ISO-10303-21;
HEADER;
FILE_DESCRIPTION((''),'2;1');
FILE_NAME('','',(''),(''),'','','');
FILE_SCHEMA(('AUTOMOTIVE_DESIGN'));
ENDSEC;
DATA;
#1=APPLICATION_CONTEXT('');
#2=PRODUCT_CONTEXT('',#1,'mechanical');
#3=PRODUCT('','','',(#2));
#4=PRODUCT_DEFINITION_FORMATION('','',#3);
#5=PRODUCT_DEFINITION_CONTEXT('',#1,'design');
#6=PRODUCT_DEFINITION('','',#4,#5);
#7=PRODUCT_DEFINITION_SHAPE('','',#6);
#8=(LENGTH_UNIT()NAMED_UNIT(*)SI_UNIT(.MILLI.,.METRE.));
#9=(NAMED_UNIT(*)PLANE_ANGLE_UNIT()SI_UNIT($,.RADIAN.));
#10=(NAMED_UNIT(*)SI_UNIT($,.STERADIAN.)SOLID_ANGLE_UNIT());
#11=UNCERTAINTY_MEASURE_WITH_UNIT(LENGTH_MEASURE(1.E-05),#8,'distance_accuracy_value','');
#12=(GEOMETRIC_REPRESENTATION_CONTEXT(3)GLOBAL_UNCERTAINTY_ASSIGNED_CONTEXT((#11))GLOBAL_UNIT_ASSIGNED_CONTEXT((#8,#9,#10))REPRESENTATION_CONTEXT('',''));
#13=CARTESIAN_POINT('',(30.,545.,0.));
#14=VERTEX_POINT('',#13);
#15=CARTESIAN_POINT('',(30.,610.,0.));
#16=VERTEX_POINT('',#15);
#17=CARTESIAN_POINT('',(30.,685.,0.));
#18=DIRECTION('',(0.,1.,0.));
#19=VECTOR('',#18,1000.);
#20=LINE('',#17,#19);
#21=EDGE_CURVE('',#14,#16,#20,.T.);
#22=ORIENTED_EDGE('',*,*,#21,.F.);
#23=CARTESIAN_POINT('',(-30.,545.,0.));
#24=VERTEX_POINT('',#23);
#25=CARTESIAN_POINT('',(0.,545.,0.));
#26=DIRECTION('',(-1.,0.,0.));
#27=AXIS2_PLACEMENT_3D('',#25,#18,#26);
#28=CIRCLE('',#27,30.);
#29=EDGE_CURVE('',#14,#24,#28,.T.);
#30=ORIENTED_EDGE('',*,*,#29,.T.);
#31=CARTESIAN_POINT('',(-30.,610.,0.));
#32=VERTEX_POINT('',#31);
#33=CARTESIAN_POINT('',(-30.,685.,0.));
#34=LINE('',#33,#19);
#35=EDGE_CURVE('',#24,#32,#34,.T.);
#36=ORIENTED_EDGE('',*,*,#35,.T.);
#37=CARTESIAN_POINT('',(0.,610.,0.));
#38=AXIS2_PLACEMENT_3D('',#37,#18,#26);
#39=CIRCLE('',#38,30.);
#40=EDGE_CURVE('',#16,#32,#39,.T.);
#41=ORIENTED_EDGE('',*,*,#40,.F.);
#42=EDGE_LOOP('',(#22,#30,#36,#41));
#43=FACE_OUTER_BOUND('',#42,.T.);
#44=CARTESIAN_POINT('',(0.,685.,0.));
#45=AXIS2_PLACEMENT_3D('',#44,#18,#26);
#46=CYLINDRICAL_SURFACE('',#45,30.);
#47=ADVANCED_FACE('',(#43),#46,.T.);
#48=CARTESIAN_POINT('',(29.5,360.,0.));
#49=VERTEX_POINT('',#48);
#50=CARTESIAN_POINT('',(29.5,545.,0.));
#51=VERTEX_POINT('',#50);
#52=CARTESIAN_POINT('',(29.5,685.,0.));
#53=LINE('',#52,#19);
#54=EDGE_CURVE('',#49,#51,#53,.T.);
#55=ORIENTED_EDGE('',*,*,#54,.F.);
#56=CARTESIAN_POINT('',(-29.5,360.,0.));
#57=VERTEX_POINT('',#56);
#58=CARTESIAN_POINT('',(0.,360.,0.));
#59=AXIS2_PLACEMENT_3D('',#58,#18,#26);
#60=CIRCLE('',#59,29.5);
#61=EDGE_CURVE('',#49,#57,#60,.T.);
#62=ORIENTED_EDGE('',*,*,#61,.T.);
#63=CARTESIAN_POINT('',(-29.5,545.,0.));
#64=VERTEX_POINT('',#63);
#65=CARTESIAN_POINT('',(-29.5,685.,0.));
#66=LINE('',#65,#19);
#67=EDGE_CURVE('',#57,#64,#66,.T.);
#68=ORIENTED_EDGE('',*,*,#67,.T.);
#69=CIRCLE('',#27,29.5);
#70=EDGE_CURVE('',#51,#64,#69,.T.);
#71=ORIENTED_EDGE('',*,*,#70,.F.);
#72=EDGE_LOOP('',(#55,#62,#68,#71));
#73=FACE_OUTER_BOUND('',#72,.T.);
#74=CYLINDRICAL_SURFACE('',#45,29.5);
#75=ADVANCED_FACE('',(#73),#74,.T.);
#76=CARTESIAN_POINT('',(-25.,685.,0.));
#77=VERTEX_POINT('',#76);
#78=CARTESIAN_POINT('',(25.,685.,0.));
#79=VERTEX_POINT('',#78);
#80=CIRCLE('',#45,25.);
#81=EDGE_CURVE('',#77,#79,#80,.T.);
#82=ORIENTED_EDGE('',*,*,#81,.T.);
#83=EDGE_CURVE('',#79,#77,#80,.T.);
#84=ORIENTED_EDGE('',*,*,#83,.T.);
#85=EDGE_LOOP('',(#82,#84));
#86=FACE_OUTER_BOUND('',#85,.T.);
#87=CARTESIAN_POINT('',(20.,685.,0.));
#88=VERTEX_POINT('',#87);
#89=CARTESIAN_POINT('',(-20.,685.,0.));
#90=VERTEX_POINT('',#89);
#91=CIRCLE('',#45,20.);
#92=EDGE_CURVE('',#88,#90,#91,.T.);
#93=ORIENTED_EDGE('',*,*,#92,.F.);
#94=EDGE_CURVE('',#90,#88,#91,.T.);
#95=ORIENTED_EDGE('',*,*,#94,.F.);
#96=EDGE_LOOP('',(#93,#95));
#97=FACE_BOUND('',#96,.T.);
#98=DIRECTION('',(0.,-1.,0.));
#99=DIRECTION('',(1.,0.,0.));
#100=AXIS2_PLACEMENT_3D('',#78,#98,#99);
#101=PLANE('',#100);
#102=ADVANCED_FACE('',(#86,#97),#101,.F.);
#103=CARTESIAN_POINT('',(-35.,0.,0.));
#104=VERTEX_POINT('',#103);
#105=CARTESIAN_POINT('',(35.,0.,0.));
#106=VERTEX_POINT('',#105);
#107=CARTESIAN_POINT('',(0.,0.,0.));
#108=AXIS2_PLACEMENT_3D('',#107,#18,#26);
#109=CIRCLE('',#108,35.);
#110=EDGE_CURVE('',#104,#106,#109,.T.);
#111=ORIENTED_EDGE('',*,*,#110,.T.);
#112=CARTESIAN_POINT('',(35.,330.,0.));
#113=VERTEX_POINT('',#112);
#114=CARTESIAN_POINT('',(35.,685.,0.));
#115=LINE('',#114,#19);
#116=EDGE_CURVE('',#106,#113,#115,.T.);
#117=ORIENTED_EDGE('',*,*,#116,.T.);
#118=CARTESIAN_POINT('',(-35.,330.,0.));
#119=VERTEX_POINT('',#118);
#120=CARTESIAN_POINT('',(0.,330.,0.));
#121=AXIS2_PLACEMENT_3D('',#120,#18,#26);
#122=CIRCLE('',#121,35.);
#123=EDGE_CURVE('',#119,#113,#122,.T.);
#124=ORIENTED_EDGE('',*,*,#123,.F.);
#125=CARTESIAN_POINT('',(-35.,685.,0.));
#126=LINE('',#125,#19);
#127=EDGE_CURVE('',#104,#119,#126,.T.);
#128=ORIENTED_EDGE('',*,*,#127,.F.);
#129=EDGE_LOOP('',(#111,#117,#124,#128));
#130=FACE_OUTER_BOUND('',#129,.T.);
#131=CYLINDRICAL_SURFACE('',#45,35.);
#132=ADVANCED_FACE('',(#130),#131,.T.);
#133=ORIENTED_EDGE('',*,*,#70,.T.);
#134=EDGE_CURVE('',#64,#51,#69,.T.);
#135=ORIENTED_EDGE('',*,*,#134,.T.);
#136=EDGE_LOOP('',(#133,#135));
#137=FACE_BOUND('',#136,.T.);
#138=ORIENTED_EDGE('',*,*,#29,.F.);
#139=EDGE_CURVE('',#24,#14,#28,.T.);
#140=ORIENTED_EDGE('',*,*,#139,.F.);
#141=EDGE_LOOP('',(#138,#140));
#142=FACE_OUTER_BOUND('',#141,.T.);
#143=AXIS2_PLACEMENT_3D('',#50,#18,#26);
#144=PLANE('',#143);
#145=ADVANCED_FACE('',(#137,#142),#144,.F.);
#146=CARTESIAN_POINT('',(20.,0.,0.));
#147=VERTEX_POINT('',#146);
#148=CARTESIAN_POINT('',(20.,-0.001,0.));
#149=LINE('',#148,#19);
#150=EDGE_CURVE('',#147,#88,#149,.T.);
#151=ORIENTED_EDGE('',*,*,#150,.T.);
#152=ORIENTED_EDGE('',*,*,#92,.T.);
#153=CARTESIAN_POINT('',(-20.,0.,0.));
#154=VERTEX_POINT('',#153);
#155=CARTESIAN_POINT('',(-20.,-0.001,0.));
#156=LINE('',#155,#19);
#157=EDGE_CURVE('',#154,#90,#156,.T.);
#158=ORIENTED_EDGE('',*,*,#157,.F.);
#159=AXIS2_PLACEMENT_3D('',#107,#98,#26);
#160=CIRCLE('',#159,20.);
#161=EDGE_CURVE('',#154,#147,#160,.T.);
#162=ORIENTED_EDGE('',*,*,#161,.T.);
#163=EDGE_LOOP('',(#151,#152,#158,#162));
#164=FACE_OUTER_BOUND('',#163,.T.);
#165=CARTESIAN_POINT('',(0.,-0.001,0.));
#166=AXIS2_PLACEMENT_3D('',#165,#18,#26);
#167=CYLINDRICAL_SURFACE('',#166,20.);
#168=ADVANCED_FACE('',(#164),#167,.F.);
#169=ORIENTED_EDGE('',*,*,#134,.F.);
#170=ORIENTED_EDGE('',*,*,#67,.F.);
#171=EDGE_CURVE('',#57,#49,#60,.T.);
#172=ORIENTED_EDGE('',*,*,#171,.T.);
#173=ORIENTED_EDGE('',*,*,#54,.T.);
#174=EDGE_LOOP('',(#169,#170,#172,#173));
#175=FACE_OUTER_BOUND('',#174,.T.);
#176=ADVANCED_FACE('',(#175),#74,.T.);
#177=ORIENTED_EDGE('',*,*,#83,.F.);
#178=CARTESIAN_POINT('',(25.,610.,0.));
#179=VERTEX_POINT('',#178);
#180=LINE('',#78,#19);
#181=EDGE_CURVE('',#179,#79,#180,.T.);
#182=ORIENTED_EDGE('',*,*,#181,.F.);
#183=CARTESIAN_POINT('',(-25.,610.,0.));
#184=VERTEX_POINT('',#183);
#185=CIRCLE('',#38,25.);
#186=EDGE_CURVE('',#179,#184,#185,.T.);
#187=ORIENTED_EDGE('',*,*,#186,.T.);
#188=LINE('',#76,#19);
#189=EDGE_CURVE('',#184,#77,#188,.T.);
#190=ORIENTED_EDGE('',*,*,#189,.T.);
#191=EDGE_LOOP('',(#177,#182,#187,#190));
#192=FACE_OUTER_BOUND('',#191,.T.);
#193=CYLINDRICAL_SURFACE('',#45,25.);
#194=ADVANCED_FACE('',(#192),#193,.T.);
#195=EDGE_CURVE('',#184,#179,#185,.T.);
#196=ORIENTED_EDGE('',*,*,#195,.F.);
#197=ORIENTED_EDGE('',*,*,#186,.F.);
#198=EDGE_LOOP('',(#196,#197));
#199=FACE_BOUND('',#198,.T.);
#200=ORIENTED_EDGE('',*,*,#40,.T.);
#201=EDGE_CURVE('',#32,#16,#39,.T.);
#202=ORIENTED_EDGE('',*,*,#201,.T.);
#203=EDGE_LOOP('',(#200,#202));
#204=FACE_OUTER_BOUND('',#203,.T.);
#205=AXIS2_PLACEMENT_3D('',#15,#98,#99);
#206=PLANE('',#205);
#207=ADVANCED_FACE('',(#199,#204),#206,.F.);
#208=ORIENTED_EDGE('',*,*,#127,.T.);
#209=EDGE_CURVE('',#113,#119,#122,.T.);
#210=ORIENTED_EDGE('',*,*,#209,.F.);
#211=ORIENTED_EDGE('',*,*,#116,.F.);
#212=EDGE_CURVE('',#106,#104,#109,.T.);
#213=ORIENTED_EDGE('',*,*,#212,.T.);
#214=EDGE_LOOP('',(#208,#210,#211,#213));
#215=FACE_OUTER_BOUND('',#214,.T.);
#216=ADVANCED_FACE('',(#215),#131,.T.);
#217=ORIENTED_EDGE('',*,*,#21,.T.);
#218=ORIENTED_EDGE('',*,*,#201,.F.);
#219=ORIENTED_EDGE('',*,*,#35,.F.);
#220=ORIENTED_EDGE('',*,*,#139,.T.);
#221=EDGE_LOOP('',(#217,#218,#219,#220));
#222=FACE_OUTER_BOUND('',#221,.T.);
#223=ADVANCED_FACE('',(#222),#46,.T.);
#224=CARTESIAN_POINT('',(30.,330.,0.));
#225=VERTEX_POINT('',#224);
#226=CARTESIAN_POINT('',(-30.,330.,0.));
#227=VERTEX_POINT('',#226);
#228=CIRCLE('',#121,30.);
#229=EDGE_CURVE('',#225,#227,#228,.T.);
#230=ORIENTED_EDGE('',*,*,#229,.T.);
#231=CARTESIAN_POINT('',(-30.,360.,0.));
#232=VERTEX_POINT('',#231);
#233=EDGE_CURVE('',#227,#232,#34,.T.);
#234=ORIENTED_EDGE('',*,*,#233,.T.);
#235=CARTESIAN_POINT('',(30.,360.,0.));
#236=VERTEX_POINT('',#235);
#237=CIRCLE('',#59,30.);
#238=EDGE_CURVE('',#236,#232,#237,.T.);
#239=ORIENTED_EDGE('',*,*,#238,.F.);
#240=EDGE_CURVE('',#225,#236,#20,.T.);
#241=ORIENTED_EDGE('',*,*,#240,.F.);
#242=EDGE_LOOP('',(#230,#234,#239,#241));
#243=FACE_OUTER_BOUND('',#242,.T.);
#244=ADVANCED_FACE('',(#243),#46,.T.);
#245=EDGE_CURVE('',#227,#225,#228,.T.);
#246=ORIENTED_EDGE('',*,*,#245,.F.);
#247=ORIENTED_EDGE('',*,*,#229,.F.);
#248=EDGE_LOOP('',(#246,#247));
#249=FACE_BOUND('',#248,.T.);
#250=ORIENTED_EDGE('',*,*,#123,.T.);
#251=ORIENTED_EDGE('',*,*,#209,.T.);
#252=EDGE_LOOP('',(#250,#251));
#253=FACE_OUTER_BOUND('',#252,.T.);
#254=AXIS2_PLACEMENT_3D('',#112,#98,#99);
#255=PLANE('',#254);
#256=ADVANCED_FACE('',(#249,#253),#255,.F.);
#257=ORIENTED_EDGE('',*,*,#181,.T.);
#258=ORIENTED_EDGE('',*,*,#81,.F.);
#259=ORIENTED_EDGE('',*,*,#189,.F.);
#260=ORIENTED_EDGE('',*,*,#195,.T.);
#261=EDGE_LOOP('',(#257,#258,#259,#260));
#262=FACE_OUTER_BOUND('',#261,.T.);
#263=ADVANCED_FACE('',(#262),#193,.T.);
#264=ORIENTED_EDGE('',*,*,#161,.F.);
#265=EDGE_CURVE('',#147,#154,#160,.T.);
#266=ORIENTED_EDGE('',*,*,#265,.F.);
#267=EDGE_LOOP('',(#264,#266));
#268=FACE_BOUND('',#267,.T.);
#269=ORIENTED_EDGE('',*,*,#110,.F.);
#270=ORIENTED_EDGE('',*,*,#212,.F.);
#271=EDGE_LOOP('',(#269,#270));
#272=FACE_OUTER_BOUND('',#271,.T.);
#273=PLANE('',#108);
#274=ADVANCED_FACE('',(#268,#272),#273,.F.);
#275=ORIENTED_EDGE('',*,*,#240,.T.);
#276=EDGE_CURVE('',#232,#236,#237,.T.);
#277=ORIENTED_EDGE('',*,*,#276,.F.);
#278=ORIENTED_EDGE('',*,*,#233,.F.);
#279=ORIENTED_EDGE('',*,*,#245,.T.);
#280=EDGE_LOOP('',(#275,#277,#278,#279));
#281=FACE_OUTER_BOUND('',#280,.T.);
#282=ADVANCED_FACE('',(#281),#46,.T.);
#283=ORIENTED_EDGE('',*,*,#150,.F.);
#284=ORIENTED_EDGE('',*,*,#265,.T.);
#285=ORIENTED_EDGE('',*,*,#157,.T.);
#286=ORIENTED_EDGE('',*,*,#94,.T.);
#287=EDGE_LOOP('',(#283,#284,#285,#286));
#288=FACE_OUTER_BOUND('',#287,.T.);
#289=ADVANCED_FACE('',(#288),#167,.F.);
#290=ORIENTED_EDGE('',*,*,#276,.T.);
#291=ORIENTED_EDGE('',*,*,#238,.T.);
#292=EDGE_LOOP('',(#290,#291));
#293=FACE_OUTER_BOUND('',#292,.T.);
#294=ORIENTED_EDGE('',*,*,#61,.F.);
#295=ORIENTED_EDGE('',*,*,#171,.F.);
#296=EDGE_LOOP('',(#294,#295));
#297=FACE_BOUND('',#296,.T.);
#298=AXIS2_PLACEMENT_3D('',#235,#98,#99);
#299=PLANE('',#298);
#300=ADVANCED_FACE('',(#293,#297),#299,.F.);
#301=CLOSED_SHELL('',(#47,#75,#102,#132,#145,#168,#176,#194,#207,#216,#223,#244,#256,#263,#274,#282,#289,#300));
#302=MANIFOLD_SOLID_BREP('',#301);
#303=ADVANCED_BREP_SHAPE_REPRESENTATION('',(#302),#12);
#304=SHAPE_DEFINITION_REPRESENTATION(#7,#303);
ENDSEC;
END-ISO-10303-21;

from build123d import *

# Parameters (mm, degrees)
CUT_EXTRUDE1_REACH = 688.786
SKETCH2_R          = 20


with BuildPart() as part:
    # Sketch1 → Revolve1 (revolve)
    with BuildSketch(Plane.XY, mode=Mode.PRIVATE) as revolve1_sk:
        Polygon((0, 0), (35, 0), (35, 330), (30, 330), (30, 360), (29.5, 360), (29.5, 545), (30, 545), (30, 610), (25, 610), (25, 685), (0, 685), align=None)
    revolve(revolve1_sk.sketch.rotate(Axis((0, 685, 0), (0, -1, 0)), 180), axis=Axis((0, 685, 0), (0, -1, 0)))

    # Sketch2 → Cut-Extrude1 (cut, up to next)
    with BuildSketch(Plane(origin=(0, 685, 0), x_dir=(1, 0, 0), z_dir=(0, 1, 0)), mode=Mode.PRIVATE) as cut_extrude1_sk1:
        with Locations(Location((0, 0, 0), (0, 0, 180))):
            Circle(SKETCH2_R)
    cut_extrude1_tool1 = extrude(cut_extrude1_sk1.sketch, amount=-CUT_EXTRUDE1_REACH, mode=Mode.PRIVATE) & part.part
    add(cut_extrude1_tool1.solids().sort_by_distance((0, 685, 0))[0], mode=Mode.SUBTRACT)


solid = part.part
